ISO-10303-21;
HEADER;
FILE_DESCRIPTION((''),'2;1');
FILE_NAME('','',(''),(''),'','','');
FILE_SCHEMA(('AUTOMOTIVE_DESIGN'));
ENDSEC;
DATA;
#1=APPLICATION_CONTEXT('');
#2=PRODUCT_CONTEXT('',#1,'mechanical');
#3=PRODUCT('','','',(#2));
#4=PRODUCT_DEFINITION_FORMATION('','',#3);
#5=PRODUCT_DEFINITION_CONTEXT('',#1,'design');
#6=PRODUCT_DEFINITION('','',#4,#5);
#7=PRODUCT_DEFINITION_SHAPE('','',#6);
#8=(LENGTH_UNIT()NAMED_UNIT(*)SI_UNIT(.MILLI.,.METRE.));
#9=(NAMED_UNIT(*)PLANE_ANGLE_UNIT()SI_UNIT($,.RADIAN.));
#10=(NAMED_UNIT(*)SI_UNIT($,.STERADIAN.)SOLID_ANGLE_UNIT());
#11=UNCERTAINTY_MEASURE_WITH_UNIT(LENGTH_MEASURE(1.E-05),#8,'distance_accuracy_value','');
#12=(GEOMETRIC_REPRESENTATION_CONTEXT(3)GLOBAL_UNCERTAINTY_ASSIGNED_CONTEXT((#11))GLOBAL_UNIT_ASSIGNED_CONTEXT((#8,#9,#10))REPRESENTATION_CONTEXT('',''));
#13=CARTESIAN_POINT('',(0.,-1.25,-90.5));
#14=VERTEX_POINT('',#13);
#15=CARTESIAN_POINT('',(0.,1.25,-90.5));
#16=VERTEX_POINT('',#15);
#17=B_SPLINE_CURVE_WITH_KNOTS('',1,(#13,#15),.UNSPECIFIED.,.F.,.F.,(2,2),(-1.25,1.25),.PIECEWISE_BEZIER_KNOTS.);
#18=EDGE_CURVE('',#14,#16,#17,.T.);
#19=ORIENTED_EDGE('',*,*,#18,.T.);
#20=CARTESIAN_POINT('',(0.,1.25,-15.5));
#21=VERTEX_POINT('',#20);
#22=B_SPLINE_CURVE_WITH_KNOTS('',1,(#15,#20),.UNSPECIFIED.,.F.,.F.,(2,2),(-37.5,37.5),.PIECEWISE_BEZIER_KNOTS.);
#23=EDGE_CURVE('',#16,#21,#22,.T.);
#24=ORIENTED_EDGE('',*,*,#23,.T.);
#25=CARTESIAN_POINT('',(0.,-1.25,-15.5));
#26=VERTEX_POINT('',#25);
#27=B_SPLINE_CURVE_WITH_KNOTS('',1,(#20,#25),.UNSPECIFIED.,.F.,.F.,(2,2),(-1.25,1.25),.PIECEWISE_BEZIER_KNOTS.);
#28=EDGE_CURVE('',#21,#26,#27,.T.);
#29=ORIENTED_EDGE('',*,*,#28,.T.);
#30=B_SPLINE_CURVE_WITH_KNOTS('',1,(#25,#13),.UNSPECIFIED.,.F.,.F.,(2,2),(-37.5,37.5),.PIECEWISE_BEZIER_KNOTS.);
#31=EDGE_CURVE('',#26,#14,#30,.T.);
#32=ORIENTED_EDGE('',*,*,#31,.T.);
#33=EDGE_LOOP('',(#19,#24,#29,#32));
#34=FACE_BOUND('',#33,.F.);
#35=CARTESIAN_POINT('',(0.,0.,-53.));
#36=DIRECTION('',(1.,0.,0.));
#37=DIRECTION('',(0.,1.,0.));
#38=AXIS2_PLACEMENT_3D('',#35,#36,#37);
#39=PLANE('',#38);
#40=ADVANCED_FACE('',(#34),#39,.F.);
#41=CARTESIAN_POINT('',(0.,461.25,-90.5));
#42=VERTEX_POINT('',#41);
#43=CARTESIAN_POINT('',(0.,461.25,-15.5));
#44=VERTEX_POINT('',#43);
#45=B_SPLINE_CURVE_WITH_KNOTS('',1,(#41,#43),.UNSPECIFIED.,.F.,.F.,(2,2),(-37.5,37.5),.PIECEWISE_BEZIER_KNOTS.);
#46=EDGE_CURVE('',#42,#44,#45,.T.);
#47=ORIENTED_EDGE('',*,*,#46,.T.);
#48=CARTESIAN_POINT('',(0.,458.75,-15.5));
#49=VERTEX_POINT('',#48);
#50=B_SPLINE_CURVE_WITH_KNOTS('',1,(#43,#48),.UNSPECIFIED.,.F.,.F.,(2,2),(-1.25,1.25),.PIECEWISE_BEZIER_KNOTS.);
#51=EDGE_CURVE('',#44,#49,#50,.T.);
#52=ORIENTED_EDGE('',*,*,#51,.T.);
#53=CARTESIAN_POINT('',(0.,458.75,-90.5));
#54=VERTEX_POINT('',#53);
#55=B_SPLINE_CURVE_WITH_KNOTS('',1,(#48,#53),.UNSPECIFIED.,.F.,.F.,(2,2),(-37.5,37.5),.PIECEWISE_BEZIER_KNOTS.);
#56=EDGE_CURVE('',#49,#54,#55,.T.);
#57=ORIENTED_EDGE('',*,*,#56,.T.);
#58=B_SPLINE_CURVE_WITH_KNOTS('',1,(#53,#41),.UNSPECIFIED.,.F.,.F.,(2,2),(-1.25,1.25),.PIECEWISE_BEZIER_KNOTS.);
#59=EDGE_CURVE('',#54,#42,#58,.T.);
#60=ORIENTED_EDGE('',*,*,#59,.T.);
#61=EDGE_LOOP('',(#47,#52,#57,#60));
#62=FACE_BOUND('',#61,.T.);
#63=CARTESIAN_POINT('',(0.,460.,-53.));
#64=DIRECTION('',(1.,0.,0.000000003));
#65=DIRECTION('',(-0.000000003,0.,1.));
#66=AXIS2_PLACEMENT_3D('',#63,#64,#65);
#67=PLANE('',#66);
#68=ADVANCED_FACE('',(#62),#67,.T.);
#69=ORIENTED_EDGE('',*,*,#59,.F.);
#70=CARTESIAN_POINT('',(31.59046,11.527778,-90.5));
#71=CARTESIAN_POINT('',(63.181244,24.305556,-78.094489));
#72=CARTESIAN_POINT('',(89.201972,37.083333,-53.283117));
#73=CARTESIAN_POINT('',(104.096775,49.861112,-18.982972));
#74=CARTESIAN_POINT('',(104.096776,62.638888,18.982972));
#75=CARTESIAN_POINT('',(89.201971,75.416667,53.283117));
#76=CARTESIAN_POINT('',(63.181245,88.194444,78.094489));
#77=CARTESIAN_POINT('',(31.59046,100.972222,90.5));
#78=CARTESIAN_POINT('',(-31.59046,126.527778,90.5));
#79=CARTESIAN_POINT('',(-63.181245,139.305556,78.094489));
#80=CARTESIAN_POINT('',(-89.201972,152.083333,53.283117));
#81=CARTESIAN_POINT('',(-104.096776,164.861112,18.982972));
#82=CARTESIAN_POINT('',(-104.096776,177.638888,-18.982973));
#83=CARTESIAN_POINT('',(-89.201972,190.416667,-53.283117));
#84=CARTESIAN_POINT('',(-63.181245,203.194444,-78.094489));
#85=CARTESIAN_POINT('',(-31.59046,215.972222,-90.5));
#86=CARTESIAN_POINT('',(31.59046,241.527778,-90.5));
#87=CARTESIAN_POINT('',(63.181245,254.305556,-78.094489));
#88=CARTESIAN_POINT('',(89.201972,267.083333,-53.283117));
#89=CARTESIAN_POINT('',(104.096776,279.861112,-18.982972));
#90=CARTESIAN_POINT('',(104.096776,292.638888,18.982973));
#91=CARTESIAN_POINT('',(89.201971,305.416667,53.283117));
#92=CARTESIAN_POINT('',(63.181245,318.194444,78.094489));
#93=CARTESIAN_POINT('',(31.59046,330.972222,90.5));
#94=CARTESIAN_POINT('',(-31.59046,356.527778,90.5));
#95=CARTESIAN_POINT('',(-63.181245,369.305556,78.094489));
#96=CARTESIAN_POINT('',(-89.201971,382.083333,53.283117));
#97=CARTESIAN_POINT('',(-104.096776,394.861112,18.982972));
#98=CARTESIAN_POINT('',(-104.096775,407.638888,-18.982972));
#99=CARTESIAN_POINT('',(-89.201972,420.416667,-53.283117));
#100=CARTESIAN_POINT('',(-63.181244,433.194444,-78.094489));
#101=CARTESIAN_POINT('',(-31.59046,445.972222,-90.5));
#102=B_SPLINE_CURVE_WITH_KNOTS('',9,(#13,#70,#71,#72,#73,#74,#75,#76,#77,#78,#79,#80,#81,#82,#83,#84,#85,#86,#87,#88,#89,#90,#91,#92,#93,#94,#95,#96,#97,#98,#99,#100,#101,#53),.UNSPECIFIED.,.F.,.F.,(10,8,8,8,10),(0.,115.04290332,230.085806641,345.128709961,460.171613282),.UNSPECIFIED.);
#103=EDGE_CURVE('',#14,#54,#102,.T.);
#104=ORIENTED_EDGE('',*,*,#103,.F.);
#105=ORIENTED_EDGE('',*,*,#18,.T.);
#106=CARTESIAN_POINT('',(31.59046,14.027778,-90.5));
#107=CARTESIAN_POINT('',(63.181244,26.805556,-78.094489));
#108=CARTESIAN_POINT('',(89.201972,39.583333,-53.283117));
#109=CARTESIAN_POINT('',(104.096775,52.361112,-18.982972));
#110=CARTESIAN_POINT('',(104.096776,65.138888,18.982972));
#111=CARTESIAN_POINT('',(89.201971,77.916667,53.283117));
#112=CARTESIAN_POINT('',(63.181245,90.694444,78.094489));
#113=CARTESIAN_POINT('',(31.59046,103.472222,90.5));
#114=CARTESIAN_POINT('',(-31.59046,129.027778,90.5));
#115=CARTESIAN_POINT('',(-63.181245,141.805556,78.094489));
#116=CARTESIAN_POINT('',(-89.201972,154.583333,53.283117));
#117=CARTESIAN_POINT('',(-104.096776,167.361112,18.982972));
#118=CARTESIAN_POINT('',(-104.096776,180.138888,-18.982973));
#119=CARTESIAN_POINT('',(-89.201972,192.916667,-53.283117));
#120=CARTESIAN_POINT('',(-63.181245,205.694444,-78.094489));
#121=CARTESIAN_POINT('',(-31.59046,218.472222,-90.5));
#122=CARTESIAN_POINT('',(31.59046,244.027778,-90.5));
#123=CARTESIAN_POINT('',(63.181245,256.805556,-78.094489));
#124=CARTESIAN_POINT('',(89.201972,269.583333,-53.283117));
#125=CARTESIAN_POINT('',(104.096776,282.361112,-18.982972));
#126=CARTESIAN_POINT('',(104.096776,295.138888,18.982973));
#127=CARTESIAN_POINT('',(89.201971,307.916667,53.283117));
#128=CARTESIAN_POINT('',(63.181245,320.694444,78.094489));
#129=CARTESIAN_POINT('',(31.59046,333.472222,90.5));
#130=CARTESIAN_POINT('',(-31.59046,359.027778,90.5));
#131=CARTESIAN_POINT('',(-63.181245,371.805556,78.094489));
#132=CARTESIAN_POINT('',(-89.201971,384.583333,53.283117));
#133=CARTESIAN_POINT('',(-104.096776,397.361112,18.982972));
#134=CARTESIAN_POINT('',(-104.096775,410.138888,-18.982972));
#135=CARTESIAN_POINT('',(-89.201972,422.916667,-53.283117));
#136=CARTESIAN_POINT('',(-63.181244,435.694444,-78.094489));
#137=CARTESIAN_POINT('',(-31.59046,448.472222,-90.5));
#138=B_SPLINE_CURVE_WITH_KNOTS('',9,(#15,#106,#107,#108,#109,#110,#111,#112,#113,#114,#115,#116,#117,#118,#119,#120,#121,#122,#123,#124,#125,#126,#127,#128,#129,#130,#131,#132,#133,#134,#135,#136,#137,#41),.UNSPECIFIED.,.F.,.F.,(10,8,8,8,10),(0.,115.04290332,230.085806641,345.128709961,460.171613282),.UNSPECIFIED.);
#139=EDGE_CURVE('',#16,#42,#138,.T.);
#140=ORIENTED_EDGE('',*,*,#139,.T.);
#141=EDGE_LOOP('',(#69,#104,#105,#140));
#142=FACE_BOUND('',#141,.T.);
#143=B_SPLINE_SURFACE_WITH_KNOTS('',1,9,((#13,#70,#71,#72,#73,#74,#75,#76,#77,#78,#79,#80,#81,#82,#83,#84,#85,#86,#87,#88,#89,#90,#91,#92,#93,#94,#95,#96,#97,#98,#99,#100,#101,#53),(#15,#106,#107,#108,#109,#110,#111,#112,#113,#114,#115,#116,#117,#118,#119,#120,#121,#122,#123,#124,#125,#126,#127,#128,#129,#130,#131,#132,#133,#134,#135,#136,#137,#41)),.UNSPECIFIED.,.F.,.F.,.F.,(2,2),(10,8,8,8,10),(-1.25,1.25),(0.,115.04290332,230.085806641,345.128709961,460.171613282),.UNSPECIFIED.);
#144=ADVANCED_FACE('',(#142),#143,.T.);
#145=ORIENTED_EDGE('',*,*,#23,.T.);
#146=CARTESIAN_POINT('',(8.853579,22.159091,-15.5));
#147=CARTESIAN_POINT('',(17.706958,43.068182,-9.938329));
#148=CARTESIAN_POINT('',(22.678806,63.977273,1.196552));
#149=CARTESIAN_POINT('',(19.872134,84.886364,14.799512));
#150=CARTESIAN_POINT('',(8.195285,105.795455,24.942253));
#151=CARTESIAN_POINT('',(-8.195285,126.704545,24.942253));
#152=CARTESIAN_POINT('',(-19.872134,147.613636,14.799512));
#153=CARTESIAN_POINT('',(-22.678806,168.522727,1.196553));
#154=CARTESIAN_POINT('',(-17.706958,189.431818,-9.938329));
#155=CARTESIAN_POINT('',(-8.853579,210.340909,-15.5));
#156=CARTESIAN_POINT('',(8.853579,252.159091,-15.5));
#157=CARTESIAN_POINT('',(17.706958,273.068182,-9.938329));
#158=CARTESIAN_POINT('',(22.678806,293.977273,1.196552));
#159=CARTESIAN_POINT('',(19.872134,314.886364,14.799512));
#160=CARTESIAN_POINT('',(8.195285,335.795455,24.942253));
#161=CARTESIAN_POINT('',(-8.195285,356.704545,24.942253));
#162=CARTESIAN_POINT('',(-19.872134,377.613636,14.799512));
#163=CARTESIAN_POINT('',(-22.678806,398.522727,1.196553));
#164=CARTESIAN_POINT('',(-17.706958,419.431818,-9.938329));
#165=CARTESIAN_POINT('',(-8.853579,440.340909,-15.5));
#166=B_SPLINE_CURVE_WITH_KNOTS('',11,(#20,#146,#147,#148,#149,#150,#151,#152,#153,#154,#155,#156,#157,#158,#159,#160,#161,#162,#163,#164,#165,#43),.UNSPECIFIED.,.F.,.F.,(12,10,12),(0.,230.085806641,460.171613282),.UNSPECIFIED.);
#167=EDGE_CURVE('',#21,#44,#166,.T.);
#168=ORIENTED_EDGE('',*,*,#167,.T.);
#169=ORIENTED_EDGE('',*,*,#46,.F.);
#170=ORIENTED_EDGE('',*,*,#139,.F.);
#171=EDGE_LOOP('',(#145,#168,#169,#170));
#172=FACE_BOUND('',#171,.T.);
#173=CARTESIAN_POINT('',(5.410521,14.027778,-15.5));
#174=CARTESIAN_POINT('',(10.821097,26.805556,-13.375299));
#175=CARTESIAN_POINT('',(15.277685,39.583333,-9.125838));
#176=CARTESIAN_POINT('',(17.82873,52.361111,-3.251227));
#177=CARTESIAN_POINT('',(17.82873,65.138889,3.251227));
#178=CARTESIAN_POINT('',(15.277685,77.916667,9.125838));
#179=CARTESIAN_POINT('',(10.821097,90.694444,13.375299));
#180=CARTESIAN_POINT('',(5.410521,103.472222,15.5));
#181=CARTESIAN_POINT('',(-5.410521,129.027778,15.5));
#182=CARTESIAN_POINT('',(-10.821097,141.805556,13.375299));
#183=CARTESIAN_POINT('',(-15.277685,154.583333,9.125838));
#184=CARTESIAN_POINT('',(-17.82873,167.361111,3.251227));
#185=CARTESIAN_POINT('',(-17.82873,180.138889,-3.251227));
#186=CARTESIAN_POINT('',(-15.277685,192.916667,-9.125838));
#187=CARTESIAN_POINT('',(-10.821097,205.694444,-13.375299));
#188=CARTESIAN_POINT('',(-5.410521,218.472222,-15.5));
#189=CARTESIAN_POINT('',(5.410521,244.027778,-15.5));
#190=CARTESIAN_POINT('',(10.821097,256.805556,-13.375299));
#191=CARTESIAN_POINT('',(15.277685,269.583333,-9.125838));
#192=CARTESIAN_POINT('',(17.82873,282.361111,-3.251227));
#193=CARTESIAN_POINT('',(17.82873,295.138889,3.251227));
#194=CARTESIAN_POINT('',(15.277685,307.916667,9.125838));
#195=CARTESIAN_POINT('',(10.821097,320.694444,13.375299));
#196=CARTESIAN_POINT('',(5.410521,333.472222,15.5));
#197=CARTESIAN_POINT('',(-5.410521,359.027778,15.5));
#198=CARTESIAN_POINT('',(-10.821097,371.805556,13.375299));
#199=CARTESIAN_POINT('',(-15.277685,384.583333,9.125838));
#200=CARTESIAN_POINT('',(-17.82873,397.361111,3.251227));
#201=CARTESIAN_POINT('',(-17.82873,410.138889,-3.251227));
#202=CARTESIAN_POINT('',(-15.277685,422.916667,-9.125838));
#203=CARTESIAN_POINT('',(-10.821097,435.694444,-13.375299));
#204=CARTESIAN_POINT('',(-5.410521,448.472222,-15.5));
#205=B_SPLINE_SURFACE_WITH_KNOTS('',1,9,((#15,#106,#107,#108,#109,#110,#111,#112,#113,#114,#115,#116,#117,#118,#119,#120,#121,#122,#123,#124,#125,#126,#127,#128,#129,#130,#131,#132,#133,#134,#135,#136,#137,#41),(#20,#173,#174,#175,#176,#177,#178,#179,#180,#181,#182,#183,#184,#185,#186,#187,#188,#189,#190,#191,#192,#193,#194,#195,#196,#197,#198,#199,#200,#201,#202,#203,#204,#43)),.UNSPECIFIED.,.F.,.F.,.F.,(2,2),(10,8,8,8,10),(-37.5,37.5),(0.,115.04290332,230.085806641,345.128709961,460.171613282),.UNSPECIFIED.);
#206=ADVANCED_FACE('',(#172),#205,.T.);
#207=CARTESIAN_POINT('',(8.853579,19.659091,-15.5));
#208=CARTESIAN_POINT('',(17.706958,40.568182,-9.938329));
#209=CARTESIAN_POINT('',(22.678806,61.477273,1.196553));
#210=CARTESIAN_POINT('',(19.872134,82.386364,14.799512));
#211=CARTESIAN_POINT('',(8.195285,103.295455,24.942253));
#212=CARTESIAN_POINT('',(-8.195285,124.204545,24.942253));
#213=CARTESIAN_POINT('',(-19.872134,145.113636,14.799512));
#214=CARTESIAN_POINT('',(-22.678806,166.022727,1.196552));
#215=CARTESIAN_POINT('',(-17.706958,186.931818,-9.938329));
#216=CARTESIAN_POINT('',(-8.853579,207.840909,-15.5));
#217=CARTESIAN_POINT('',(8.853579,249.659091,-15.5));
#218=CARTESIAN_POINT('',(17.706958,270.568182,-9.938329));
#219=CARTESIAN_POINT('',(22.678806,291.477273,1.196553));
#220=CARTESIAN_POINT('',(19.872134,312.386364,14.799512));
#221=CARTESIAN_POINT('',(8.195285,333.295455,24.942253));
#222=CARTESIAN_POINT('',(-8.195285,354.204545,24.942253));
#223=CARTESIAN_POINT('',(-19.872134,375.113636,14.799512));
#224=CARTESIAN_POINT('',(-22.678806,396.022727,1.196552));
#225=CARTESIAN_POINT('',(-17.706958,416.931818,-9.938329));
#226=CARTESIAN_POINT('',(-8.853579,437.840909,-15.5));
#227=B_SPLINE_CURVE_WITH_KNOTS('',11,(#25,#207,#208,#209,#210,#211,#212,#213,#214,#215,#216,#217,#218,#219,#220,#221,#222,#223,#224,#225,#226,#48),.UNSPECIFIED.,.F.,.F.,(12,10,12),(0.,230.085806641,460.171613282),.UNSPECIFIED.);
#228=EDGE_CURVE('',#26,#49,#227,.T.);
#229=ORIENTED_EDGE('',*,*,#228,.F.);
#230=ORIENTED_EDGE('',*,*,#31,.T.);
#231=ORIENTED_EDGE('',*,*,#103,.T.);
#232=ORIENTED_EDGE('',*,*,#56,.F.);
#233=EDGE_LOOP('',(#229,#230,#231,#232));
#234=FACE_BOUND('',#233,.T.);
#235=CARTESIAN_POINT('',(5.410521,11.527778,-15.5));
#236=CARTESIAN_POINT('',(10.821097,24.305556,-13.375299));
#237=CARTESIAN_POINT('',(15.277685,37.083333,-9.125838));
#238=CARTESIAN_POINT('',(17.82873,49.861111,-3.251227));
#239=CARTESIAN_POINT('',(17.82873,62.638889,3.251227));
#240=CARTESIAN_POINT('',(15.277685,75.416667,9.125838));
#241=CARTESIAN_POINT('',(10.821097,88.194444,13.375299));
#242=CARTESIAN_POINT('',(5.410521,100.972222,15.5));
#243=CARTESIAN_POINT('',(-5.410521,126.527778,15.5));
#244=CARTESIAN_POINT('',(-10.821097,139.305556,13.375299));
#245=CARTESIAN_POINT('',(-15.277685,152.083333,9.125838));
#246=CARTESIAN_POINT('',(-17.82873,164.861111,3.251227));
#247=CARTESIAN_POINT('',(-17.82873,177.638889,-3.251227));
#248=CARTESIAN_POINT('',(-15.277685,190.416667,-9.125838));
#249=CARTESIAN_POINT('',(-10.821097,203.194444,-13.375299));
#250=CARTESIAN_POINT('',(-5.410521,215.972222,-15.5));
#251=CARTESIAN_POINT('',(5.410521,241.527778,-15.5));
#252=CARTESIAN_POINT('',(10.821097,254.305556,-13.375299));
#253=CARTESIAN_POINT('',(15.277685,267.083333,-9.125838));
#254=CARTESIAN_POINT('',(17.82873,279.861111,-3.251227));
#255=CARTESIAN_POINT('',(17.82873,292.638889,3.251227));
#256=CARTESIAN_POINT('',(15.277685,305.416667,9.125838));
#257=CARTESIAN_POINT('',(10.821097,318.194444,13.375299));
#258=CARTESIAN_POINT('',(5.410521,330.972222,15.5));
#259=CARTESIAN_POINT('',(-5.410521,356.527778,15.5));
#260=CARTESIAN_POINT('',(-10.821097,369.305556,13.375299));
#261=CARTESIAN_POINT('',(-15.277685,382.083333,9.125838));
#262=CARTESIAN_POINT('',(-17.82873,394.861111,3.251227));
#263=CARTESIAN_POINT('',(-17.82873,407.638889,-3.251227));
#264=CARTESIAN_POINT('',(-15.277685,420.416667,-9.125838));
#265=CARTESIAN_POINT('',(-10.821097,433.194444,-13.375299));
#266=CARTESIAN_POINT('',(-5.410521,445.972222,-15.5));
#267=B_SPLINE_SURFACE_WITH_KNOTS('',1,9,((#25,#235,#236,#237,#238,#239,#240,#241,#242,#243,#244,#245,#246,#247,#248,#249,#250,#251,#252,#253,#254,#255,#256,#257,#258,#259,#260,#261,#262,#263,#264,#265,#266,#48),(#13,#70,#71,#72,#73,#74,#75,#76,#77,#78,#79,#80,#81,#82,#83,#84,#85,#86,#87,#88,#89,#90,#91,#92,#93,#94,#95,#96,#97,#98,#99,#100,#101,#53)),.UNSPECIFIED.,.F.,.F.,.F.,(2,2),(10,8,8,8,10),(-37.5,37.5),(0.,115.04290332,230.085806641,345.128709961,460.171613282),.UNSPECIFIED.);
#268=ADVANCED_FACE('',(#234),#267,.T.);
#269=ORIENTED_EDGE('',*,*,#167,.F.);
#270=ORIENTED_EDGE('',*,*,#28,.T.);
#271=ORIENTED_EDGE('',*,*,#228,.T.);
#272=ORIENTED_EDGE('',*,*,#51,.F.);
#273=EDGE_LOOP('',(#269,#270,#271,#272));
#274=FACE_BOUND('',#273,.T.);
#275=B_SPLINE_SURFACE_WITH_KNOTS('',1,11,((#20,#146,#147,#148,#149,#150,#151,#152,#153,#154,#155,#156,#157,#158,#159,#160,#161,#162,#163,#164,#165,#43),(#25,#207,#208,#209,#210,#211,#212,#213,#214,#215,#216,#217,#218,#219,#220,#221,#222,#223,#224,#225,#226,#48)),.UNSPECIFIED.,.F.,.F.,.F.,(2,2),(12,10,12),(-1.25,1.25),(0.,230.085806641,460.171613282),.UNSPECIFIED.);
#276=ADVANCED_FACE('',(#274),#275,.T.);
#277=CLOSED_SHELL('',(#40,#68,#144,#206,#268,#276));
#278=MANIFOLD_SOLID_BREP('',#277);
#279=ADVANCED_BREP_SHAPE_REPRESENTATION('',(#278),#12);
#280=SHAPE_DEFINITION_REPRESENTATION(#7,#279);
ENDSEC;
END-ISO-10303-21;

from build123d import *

# Parameters (mm, degrees)
SWEEP_14_PITCH       = 230
SWEEP_14_HEIGHT      = 460
SWEEP_14_RADIUS      = 15
SWEEP_14_START_ANGLE = -180
SKETCH_11_W          = 75
SKETCH_11_H          = 2.5


with BuildPart() as part:
    # 扫描14: sweep along a helix
    with BuildLine() as sweep_14_path:
        add(Helix(SWEEP_14_PITCH, SWEEP_14_HEIGHT, SWEEP_14_RADIUS, center=(0, 0, 0), direction=(0, 1, 0), lefthand=True, mode=Mode.PRIVATE).rotate(Axis((0, 0, 0), (0, 1, 0)), SWEEP_14_START_ANGLE))
    # 草图11 → 扫描14 (sweep)
    with BuildSketch(Plane(origin=(0, 0, 0), x_dir=(0, 0, -1), z_dir=(1, 0, 0))):
        with Locations((53, 0)):
            Rectangle(SKETCH_11_W, SKETCH_11_H)
    sweep(path=sweep_14_path.line, is_frenet=True)


solid = part.part
